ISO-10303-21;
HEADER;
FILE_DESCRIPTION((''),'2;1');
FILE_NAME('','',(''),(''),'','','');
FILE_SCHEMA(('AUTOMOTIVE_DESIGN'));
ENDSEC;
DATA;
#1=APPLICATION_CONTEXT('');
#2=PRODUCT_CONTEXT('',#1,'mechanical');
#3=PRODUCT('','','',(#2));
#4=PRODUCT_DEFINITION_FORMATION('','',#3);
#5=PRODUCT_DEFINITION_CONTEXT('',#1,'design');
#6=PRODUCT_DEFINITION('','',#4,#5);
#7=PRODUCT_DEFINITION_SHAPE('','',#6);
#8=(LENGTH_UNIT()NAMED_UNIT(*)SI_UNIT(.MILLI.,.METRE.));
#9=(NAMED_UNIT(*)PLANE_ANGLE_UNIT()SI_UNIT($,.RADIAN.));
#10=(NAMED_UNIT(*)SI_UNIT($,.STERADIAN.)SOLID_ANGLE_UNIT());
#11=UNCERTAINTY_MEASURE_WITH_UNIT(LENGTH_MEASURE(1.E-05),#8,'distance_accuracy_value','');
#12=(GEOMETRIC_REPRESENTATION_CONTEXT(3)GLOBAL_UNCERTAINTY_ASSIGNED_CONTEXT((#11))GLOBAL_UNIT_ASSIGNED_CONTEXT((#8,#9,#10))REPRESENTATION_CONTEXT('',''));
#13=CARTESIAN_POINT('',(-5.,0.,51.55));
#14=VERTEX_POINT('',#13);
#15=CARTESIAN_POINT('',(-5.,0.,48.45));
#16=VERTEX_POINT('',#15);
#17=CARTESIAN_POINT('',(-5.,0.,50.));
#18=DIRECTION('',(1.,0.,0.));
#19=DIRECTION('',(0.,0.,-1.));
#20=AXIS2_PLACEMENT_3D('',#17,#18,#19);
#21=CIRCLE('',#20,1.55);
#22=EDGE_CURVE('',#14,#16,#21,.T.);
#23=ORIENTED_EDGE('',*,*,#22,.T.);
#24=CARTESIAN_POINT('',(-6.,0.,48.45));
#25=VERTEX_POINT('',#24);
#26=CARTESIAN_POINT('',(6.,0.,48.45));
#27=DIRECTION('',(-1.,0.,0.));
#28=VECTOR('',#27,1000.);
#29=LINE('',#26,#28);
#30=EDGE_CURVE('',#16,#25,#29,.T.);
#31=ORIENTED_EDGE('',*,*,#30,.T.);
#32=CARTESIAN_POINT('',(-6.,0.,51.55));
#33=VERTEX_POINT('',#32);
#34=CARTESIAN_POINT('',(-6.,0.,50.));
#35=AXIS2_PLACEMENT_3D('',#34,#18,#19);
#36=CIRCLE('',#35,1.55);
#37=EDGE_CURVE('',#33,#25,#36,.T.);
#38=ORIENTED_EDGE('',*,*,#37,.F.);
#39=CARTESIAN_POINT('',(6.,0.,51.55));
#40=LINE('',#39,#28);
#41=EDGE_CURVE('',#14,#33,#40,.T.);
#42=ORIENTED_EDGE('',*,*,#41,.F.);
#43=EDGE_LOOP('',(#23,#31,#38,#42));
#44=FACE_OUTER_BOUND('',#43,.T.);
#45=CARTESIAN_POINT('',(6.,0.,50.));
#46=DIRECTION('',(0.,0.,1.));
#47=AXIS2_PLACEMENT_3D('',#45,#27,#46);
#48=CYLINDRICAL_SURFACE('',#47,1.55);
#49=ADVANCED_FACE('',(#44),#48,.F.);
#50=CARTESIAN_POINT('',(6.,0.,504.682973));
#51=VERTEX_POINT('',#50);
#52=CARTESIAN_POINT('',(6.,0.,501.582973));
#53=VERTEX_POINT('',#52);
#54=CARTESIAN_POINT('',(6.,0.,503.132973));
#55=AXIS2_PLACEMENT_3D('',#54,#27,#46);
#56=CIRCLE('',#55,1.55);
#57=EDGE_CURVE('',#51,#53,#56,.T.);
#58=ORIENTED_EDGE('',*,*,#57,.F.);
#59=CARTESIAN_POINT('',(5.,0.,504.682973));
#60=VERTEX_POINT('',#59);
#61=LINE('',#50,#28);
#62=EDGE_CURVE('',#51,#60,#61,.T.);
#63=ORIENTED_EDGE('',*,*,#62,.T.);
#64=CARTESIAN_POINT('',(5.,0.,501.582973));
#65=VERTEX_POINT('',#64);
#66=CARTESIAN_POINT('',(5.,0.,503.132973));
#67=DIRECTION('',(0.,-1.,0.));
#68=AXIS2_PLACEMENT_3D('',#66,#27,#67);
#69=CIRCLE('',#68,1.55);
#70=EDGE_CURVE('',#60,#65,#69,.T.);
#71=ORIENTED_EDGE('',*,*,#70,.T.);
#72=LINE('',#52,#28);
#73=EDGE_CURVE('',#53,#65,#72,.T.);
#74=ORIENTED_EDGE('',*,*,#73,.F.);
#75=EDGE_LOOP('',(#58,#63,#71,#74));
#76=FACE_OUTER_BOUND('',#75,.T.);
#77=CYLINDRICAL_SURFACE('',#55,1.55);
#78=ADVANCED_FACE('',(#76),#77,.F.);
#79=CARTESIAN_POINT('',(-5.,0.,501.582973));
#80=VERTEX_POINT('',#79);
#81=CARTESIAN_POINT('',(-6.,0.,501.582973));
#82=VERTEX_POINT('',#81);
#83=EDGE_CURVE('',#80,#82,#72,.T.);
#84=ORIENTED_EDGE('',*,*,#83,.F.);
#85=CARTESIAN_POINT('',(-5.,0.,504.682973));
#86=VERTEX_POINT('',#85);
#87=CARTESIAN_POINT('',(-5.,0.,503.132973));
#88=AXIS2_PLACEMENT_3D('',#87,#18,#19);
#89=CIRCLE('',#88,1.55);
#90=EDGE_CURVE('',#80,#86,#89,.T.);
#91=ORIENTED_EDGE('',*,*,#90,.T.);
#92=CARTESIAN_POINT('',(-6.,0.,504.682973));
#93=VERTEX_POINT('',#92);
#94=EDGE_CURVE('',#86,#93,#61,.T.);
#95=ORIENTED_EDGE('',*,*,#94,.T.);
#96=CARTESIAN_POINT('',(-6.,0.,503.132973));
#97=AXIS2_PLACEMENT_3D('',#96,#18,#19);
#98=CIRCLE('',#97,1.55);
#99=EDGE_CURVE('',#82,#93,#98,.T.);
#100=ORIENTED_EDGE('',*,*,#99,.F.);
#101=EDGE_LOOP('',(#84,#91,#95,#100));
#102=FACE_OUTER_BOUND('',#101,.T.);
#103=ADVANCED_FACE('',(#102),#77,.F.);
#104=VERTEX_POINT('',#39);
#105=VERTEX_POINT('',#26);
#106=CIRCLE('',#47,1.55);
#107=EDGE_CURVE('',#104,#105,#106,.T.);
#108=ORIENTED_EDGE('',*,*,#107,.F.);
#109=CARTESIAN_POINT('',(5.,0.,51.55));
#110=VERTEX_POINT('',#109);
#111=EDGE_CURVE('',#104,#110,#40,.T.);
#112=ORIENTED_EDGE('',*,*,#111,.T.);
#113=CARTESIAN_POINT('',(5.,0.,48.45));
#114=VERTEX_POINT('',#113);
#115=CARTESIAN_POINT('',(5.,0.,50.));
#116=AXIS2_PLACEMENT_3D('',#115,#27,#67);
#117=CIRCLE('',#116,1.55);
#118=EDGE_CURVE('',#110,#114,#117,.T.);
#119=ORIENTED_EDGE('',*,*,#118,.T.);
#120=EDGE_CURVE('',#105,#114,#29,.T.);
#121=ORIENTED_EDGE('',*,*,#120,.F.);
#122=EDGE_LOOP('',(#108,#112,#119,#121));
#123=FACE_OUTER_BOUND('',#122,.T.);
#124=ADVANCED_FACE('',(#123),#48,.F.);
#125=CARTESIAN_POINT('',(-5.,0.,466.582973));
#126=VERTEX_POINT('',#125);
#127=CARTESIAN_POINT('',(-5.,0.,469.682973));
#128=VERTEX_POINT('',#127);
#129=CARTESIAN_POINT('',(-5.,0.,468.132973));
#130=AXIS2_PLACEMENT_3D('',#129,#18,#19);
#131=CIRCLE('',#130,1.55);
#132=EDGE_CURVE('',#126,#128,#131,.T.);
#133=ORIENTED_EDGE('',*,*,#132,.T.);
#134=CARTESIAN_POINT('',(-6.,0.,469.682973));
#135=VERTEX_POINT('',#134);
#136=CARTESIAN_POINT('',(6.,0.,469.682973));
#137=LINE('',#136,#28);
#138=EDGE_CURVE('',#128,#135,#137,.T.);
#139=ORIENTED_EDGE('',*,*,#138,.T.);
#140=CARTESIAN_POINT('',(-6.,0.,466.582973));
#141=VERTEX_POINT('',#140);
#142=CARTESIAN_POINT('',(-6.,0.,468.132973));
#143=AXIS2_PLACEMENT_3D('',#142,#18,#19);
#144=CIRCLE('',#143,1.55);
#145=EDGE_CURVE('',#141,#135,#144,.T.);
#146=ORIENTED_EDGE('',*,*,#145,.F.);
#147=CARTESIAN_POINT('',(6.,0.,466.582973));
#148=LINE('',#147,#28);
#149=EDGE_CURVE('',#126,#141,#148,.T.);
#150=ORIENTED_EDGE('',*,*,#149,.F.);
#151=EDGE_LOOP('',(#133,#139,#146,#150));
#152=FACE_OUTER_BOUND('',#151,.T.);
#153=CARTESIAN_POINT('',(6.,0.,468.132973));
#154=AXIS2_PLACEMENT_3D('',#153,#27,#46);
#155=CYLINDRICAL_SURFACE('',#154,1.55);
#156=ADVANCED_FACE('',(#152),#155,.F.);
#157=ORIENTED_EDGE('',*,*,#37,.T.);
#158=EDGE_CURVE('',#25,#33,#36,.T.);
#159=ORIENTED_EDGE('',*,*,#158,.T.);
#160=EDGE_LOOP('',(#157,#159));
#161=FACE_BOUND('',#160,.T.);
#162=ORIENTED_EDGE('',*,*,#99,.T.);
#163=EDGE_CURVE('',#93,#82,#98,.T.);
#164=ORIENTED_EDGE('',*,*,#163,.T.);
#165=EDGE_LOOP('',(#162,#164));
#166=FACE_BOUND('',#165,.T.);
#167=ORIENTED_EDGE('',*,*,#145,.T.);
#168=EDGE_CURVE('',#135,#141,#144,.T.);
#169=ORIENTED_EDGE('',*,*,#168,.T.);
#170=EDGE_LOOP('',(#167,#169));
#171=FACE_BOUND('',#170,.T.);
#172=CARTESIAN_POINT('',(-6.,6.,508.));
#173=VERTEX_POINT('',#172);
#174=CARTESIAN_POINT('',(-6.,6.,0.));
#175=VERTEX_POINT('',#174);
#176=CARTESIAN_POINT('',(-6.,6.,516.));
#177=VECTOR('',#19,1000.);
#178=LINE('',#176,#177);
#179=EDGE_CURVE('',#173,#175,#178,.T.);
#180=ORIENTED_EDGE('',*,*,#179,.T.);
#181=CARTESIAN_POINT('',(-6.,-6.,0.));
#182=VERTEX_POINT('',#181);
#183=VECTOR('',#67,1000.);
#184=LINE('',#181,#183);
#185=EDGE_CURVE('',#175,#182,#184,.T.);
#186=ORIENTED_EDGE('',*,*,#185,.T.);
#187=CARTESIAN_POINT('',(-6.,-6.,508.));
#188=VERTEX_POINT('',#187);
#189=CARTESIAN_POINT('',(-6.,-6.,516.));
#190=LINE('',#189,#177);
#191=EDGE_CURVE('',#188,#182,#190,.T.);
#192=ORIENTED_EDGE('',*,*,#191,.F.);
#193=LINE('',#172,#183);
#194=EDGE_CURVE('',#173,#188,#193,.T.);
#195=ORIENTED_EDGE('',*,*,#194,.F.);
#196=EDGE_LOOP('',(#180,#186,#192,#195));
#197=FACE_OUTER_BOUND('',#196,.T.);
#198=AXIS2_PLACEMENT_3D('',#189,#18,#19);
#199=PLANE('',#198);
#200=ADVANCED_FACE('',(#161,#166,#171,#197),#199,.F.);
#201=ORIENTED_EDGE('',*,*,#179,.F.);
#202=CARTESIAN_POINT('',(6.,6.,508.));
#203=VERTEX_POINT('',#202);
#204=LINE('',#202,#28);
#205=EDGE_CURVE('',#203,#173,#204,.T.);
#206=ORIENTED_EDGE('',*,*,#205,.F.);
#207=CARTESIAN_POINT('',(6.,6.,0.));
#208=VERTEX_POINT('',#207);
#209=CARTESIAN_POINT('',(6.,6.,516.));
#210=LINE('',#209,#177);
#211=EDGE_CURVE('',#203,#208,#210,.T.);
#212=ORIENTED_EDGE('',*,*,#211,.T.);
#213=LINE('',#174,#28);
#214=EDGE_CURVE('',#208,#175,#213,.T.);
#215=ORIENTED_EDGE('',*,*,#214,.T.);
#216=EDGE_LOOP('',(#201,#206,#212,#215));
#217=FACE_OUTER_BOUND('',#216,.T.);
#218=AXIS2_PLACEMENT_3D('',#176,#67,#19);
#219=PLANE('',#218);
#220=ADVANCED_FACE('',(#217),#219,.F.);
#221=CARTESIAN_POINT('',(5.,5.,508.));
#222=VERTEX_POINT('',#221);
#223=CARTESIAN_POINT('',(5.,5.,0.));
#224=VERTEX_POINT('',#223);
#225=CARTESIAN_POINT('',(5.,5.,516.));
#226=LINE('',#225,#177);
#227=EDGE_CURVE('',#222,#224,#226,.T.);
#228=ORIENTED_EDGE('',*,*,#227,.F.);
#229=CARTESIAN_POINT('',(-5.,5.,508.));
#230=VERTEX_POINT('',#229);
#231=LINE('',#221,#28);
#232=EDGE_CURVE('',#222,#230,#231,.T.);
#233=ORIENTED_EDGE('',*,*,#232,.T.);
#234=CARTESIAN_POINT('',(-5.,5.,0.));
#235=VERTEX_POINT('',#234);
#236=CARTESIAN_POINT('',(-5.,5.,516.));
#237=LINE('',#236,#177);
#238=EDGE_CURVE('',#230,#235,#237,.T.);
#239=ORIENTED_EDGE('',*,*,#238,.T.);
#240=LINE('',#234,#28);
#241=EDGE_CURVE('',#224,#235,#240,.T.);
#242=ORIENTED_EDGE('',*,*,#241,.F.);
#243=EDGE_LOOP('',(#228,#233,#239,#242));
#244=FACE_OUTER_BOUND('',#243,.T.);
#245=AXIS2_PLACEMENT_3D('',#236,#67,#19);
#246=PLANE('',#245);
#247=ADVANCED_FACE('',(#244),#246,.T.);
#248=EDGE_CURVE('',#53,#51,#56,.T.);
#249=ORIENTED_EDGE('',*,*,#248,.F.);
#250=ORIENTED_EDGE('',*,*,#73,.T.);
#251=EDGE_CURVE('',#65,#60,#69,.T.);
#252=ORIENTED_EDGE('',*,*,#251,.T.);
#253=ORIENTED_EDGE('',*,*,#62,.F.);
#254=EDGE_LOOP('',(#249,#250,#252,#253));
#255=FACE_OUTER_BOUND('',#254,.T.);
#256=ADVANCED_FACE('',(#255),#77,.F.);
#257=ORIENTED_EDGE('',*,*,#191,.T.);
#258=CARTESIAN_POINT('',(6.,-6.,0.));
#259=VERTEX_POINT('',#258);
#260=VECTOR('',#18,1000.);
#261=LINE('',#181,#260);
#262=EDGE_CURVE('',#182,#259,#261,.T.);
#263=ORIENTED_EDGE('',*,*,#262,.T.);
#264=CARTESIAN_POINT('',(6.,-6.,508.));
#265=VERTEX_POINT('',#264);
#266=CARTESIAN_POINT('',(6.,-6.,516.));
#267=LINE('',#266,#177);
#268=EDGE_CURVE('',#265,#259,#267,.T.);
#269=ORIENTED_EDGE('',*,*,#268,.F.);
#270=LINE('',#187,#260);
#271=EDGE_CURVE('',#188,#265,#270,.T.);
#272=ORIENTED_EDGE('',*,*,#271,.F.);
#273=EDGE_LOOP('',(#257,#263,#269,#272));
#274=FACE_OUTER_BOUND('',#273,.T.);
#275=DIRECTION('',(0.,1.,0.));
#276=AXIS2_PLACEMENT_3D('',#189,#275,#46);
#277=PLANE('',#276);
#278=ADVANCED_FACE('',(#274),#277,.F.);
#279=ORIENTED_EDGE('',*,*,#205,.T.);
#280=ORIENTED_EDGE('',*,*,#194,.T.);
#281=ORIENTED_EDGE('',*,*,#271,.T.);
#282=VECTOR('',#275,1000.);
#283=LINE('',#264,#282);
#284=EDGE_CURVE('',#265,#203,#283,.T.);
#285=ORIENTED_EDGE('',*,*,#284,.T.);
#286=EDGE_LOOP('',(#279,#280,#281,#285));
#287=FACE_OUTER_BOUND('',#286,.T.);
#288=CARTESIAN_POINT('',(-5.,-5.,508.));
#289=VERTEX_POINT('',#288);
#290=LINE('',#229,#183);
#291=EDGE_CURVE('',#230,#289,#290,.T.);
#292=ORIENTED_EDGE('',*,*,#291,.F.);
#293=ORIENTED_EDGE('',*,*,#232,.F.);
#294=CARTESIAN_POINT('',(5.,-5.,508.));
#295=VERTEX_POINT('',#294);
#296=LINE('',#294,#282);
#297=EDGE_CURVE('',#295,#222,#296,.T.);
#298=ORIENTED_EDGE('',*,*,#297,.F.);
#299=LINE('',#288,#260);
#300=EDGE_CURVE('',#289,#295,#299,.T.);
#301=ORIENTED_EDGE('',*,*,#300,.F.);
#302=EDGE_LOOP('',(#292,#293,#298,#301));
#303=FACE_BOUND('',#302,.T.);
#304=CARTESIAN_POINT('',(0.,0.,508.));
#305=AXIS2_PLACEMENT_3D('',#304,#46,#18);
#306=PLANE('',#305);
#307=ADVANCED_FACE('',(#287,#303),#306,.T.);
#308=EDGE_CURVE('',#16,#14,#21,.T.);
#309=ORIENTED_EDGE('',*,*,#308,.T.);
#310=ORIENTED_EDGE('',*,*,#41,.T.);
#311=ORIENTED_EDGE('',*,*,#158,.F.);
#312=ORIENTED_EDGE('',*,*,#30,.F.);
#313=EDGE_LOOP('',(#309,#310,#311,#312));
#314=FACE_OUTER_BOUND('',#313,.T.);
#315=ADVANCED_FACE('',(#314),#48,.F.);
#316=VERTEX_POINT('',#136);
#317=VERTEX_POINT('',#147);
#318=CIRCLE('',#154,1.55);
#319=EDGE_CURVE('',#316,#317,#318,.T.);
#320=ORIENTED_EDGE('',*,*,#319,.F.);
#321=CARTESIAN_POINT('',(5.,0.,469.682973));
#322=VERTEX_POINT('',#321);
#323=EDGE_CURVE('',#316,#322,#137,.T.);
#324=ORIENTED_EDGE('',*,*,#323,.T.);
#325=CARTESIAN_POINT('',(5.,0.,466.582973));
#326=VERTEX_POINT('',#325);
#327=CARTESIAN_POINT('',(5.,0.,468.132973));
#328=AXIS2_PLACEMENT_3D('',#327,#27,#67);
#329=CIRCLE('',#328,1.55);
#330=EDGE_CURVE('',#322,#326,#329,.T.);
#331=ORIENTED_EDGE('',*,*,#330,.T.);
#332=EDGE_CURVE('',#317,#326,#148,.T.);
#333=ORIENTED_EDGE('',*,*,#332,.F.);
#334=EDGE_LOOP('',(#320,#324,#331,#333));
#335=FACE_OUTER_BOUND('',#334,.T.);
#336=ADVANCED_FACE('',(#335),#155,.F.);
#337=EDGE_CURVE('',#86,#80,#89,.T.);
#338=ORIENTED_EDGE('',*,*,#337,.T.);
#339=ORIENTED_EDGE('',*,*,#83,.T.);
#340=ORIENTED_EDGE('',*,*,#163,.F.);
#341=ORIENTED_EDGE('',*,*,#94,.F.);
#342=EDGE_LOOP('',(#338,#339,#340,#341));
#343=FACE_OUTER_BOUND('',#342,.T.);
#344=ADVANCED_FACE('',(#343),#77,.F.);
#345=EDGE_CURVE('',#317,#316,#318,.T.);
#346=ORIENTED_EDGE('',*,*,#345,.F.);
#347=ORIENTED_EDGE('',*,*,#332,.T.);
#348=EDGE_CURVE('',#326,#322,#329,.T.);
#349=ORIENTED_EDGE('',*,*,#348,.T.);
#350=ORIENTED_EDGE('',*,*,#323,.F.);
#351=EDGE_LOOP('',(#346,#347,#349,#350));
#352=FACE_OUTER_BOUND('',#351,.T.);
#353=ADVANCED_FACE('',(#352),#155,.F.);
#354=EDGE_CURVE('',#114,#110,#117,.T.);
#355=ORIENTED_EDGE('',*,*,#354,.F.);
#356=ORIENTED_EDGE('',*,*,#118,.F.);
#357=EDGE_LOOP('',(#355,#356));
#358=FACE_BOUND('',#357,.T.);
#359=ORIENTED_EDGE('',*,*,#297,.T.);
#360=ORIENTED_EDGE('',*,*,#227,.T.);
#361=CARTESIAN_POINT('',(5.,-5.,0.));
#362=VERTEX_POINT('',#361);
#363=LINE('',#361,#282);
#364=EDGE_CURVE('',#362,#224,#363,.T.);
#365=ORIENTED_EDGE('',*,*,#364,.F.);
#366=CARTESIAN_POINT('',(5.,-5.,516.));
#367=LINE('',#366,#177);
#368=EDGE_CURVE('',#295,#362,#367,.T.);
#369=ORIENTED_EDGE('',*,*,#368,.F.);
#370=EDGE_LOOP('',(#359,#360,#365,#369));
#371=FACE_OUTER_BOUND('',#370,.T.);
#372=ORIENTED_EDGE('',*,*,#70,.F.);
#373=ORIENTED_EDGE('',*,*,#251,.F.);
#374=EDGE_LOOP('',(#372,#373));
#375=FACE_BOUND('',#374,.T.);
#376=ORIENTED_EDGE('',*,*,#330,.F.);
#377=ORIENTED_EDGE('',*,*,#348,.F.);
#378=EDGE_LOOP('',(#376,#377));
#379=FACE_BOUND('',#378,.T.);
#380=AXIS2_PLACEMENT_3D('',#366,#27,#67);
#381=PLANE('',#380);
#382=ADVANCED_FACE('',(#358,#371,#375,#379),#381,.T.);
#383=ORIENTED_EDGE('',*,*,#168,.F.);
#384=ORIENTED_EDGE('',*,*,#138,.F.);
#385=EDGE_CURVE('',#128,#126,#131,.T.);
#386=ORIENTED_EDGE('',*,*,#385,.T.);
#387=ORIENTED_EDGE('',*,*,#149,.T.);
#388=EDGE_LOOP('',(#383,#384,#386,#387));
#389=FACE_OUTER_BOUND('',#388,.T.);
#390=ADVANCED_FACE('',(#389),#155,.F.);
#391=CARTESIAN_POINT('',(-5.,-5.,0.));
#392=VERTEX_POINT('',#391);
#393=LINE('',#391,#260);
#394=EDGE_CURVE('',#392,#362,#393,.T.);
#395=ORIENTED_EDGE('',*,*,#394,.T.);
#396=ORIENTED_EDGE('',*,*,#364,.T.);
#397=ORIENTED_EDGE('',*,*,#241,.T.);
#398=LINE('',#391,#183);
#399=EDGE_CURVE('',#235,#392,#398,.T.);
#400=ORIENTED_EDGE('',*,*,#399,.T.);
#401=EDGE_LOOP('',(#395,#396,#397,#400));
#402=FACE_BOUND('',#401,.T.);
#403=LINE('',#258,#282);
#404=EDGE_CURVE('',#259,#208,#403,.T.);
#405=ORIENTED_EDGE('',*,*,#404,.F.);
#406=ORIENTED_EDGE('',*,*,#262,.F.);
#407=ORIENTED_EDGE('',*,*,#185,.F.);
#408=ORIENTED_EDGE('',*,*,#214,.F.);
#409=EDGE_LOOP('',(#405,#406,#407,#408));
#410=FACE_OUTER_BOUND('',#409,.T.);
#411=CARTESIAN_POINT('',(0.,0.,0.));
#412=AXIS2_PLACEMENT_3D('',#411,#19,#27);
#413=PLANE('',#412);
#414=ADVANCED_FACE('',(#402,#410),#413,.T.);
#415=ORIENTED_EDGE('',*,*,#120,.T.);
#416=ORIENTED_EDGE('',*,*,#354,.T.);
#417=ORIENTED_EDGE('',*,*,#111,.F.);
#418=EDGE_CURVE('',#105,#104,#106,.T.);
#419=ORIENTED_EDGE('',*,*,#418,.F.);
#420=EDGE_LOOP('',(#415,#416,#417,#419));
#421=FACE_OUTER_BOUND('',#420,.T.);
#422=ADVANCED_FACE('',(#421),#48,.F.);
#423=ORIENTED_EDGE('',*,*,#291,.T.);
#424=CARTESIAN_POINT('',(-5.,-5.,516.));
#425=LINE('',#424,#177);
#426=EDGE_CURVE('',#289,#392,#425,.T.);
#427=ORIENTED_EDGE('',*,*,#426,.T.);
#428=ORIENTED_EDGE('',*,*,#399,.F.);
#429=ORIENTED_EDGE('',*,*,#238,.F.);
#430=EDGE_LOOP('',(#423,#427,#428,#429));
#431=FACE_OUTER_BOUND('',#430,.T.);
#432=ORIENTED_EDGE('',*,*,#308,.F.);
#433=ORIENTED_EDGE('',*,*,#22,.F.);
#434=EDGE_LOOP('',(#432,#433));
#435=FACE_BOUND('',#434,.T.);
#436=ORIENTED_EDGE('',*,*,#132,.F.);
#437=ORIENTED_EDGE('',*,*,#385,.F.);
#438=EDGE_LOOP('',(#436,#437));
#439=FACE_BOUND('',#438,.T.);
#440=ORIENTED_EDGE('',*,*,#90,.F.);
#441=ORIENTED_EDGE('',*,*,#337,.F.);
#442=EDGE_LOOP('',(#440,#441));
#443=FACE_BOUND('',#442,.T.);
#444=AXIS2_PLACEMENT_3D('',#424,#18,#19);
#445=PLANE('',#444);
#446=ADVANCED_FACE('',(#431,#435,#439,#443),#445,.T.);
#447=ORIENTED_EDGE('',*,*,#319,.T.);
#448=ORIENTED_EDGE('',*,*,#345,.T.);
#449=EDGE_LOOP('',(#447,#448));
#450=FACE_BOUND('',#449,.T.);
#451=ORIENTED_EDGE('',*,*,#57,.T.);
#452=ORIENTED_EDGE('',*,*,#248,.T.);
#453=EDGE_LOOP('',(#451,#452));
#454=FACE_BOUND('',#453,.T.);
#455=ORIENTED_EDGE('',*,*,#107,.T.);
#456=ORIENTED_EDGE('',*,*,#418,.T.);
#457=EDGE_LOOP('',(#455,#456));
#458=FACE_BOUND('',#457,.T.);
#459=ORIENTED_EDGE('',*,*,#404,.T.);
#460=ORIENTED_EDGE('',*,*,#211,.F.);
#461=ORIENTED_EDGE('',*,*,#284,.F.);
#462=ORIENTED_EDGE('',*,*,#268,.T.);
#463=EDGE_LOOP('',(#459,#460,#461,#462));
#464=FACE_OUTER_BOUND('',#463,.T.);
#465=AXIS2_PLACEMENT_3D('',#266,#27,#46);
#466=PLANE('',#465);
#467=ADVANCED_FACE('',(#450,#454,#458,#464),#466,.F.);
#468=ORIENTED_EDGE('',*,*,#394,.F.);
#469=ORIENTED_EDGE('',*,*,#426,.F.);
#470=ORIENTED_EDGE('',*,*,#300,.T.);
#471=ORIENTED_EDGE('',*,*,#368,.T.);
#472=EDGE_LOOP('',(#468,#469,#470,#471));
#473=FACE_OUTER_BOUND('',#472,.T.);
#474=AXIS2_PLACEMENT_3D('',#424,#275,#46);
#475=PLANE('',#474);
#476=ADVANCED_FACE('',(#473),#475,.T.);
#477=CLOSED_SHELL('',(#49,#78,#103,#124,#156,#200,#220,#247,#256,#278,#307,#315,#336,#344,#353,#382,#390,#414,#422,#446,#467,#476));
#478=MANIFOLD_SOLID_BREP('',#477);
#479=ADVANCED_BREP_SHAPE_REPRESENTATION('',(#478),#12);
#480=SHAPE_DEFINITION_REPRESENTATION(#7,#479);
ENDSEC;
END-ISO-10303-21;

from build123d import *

# Parameters (mm, degrees)
SKETCH_1_W               = 12
SKETCH_1_H               = 12
SKETCH_1_W_2             = 10
SKETCH_1_H_2             = 10
EXTRUDE_1_DEPTH          = 516
CUT_EXTRUDE_1_DEPTH      = 517.174389136
CUT_EXTRUDE_1_DEPTH_BACK = 517.174389136
SKETCH_2_R               = 1.55
SKETCH_3_W               = 12
SKETCH_3_H               = 12
SKETCH_3_W_2             = 10
SKETCH_3_H_2             = 10
CUT_EXTRUDE_2_DEPTH      = 8


with BuildPart() as part:
    # 草图1 → 凸台-拉伸1 (new body)
    with BuildSketch(Plane.XY):
        Rectangle(SKETCH_1_W, SKETCH_1_H)
        Rectangle(SKETCH_1_W_2, SKETCH_1_H_2, mode=Mode.SUBTRACT)
    extrude(amount=EXTRUDE_1_DEPTH)

    # 草图2 → 切除-拉伸1 (cut, two sides: drawn at the far end of the back side and taken through both)
    with BuildSketch(Plane.ZY.offset(6).offset(-CUT_EXTRUDE_1_DEPTH_BACK)):
        with Locations(Location((50, 0, 0), (0, 0, 180))):
            Circle(SKETCH_2_R)
        with Locations(Location((468.132973417, 0, 0), (0, 0, 180))):
            Circle(SKETCH_2_R)
        with Locations(Location((503.132973417, 0, 0), (0, 0, 180))):
            Circle(SKETCH_2_R)
    extrude(amount=CUT_EXTRUDE_1_DEPTH + CUT_EXTRUDE_1_DEPTH_BACK, mode=Mode.SUBTRACT)

    # 草图3 → 切除-拉伸2 (cut)
    with BuildSketch(Plane.XY.offset(516)):
        Rectangle(SKETCH_3_W, SKETCH_3_H)
        Rectangle(SKETCH_3_W_2, SKETCH_3_H_2, mode=Mode.SUBTRACT)
    extrude(amount=-CUT_EXTRUDE_2_DEPTH, mode=Mode.SUBTRACT)


solid = part.part
